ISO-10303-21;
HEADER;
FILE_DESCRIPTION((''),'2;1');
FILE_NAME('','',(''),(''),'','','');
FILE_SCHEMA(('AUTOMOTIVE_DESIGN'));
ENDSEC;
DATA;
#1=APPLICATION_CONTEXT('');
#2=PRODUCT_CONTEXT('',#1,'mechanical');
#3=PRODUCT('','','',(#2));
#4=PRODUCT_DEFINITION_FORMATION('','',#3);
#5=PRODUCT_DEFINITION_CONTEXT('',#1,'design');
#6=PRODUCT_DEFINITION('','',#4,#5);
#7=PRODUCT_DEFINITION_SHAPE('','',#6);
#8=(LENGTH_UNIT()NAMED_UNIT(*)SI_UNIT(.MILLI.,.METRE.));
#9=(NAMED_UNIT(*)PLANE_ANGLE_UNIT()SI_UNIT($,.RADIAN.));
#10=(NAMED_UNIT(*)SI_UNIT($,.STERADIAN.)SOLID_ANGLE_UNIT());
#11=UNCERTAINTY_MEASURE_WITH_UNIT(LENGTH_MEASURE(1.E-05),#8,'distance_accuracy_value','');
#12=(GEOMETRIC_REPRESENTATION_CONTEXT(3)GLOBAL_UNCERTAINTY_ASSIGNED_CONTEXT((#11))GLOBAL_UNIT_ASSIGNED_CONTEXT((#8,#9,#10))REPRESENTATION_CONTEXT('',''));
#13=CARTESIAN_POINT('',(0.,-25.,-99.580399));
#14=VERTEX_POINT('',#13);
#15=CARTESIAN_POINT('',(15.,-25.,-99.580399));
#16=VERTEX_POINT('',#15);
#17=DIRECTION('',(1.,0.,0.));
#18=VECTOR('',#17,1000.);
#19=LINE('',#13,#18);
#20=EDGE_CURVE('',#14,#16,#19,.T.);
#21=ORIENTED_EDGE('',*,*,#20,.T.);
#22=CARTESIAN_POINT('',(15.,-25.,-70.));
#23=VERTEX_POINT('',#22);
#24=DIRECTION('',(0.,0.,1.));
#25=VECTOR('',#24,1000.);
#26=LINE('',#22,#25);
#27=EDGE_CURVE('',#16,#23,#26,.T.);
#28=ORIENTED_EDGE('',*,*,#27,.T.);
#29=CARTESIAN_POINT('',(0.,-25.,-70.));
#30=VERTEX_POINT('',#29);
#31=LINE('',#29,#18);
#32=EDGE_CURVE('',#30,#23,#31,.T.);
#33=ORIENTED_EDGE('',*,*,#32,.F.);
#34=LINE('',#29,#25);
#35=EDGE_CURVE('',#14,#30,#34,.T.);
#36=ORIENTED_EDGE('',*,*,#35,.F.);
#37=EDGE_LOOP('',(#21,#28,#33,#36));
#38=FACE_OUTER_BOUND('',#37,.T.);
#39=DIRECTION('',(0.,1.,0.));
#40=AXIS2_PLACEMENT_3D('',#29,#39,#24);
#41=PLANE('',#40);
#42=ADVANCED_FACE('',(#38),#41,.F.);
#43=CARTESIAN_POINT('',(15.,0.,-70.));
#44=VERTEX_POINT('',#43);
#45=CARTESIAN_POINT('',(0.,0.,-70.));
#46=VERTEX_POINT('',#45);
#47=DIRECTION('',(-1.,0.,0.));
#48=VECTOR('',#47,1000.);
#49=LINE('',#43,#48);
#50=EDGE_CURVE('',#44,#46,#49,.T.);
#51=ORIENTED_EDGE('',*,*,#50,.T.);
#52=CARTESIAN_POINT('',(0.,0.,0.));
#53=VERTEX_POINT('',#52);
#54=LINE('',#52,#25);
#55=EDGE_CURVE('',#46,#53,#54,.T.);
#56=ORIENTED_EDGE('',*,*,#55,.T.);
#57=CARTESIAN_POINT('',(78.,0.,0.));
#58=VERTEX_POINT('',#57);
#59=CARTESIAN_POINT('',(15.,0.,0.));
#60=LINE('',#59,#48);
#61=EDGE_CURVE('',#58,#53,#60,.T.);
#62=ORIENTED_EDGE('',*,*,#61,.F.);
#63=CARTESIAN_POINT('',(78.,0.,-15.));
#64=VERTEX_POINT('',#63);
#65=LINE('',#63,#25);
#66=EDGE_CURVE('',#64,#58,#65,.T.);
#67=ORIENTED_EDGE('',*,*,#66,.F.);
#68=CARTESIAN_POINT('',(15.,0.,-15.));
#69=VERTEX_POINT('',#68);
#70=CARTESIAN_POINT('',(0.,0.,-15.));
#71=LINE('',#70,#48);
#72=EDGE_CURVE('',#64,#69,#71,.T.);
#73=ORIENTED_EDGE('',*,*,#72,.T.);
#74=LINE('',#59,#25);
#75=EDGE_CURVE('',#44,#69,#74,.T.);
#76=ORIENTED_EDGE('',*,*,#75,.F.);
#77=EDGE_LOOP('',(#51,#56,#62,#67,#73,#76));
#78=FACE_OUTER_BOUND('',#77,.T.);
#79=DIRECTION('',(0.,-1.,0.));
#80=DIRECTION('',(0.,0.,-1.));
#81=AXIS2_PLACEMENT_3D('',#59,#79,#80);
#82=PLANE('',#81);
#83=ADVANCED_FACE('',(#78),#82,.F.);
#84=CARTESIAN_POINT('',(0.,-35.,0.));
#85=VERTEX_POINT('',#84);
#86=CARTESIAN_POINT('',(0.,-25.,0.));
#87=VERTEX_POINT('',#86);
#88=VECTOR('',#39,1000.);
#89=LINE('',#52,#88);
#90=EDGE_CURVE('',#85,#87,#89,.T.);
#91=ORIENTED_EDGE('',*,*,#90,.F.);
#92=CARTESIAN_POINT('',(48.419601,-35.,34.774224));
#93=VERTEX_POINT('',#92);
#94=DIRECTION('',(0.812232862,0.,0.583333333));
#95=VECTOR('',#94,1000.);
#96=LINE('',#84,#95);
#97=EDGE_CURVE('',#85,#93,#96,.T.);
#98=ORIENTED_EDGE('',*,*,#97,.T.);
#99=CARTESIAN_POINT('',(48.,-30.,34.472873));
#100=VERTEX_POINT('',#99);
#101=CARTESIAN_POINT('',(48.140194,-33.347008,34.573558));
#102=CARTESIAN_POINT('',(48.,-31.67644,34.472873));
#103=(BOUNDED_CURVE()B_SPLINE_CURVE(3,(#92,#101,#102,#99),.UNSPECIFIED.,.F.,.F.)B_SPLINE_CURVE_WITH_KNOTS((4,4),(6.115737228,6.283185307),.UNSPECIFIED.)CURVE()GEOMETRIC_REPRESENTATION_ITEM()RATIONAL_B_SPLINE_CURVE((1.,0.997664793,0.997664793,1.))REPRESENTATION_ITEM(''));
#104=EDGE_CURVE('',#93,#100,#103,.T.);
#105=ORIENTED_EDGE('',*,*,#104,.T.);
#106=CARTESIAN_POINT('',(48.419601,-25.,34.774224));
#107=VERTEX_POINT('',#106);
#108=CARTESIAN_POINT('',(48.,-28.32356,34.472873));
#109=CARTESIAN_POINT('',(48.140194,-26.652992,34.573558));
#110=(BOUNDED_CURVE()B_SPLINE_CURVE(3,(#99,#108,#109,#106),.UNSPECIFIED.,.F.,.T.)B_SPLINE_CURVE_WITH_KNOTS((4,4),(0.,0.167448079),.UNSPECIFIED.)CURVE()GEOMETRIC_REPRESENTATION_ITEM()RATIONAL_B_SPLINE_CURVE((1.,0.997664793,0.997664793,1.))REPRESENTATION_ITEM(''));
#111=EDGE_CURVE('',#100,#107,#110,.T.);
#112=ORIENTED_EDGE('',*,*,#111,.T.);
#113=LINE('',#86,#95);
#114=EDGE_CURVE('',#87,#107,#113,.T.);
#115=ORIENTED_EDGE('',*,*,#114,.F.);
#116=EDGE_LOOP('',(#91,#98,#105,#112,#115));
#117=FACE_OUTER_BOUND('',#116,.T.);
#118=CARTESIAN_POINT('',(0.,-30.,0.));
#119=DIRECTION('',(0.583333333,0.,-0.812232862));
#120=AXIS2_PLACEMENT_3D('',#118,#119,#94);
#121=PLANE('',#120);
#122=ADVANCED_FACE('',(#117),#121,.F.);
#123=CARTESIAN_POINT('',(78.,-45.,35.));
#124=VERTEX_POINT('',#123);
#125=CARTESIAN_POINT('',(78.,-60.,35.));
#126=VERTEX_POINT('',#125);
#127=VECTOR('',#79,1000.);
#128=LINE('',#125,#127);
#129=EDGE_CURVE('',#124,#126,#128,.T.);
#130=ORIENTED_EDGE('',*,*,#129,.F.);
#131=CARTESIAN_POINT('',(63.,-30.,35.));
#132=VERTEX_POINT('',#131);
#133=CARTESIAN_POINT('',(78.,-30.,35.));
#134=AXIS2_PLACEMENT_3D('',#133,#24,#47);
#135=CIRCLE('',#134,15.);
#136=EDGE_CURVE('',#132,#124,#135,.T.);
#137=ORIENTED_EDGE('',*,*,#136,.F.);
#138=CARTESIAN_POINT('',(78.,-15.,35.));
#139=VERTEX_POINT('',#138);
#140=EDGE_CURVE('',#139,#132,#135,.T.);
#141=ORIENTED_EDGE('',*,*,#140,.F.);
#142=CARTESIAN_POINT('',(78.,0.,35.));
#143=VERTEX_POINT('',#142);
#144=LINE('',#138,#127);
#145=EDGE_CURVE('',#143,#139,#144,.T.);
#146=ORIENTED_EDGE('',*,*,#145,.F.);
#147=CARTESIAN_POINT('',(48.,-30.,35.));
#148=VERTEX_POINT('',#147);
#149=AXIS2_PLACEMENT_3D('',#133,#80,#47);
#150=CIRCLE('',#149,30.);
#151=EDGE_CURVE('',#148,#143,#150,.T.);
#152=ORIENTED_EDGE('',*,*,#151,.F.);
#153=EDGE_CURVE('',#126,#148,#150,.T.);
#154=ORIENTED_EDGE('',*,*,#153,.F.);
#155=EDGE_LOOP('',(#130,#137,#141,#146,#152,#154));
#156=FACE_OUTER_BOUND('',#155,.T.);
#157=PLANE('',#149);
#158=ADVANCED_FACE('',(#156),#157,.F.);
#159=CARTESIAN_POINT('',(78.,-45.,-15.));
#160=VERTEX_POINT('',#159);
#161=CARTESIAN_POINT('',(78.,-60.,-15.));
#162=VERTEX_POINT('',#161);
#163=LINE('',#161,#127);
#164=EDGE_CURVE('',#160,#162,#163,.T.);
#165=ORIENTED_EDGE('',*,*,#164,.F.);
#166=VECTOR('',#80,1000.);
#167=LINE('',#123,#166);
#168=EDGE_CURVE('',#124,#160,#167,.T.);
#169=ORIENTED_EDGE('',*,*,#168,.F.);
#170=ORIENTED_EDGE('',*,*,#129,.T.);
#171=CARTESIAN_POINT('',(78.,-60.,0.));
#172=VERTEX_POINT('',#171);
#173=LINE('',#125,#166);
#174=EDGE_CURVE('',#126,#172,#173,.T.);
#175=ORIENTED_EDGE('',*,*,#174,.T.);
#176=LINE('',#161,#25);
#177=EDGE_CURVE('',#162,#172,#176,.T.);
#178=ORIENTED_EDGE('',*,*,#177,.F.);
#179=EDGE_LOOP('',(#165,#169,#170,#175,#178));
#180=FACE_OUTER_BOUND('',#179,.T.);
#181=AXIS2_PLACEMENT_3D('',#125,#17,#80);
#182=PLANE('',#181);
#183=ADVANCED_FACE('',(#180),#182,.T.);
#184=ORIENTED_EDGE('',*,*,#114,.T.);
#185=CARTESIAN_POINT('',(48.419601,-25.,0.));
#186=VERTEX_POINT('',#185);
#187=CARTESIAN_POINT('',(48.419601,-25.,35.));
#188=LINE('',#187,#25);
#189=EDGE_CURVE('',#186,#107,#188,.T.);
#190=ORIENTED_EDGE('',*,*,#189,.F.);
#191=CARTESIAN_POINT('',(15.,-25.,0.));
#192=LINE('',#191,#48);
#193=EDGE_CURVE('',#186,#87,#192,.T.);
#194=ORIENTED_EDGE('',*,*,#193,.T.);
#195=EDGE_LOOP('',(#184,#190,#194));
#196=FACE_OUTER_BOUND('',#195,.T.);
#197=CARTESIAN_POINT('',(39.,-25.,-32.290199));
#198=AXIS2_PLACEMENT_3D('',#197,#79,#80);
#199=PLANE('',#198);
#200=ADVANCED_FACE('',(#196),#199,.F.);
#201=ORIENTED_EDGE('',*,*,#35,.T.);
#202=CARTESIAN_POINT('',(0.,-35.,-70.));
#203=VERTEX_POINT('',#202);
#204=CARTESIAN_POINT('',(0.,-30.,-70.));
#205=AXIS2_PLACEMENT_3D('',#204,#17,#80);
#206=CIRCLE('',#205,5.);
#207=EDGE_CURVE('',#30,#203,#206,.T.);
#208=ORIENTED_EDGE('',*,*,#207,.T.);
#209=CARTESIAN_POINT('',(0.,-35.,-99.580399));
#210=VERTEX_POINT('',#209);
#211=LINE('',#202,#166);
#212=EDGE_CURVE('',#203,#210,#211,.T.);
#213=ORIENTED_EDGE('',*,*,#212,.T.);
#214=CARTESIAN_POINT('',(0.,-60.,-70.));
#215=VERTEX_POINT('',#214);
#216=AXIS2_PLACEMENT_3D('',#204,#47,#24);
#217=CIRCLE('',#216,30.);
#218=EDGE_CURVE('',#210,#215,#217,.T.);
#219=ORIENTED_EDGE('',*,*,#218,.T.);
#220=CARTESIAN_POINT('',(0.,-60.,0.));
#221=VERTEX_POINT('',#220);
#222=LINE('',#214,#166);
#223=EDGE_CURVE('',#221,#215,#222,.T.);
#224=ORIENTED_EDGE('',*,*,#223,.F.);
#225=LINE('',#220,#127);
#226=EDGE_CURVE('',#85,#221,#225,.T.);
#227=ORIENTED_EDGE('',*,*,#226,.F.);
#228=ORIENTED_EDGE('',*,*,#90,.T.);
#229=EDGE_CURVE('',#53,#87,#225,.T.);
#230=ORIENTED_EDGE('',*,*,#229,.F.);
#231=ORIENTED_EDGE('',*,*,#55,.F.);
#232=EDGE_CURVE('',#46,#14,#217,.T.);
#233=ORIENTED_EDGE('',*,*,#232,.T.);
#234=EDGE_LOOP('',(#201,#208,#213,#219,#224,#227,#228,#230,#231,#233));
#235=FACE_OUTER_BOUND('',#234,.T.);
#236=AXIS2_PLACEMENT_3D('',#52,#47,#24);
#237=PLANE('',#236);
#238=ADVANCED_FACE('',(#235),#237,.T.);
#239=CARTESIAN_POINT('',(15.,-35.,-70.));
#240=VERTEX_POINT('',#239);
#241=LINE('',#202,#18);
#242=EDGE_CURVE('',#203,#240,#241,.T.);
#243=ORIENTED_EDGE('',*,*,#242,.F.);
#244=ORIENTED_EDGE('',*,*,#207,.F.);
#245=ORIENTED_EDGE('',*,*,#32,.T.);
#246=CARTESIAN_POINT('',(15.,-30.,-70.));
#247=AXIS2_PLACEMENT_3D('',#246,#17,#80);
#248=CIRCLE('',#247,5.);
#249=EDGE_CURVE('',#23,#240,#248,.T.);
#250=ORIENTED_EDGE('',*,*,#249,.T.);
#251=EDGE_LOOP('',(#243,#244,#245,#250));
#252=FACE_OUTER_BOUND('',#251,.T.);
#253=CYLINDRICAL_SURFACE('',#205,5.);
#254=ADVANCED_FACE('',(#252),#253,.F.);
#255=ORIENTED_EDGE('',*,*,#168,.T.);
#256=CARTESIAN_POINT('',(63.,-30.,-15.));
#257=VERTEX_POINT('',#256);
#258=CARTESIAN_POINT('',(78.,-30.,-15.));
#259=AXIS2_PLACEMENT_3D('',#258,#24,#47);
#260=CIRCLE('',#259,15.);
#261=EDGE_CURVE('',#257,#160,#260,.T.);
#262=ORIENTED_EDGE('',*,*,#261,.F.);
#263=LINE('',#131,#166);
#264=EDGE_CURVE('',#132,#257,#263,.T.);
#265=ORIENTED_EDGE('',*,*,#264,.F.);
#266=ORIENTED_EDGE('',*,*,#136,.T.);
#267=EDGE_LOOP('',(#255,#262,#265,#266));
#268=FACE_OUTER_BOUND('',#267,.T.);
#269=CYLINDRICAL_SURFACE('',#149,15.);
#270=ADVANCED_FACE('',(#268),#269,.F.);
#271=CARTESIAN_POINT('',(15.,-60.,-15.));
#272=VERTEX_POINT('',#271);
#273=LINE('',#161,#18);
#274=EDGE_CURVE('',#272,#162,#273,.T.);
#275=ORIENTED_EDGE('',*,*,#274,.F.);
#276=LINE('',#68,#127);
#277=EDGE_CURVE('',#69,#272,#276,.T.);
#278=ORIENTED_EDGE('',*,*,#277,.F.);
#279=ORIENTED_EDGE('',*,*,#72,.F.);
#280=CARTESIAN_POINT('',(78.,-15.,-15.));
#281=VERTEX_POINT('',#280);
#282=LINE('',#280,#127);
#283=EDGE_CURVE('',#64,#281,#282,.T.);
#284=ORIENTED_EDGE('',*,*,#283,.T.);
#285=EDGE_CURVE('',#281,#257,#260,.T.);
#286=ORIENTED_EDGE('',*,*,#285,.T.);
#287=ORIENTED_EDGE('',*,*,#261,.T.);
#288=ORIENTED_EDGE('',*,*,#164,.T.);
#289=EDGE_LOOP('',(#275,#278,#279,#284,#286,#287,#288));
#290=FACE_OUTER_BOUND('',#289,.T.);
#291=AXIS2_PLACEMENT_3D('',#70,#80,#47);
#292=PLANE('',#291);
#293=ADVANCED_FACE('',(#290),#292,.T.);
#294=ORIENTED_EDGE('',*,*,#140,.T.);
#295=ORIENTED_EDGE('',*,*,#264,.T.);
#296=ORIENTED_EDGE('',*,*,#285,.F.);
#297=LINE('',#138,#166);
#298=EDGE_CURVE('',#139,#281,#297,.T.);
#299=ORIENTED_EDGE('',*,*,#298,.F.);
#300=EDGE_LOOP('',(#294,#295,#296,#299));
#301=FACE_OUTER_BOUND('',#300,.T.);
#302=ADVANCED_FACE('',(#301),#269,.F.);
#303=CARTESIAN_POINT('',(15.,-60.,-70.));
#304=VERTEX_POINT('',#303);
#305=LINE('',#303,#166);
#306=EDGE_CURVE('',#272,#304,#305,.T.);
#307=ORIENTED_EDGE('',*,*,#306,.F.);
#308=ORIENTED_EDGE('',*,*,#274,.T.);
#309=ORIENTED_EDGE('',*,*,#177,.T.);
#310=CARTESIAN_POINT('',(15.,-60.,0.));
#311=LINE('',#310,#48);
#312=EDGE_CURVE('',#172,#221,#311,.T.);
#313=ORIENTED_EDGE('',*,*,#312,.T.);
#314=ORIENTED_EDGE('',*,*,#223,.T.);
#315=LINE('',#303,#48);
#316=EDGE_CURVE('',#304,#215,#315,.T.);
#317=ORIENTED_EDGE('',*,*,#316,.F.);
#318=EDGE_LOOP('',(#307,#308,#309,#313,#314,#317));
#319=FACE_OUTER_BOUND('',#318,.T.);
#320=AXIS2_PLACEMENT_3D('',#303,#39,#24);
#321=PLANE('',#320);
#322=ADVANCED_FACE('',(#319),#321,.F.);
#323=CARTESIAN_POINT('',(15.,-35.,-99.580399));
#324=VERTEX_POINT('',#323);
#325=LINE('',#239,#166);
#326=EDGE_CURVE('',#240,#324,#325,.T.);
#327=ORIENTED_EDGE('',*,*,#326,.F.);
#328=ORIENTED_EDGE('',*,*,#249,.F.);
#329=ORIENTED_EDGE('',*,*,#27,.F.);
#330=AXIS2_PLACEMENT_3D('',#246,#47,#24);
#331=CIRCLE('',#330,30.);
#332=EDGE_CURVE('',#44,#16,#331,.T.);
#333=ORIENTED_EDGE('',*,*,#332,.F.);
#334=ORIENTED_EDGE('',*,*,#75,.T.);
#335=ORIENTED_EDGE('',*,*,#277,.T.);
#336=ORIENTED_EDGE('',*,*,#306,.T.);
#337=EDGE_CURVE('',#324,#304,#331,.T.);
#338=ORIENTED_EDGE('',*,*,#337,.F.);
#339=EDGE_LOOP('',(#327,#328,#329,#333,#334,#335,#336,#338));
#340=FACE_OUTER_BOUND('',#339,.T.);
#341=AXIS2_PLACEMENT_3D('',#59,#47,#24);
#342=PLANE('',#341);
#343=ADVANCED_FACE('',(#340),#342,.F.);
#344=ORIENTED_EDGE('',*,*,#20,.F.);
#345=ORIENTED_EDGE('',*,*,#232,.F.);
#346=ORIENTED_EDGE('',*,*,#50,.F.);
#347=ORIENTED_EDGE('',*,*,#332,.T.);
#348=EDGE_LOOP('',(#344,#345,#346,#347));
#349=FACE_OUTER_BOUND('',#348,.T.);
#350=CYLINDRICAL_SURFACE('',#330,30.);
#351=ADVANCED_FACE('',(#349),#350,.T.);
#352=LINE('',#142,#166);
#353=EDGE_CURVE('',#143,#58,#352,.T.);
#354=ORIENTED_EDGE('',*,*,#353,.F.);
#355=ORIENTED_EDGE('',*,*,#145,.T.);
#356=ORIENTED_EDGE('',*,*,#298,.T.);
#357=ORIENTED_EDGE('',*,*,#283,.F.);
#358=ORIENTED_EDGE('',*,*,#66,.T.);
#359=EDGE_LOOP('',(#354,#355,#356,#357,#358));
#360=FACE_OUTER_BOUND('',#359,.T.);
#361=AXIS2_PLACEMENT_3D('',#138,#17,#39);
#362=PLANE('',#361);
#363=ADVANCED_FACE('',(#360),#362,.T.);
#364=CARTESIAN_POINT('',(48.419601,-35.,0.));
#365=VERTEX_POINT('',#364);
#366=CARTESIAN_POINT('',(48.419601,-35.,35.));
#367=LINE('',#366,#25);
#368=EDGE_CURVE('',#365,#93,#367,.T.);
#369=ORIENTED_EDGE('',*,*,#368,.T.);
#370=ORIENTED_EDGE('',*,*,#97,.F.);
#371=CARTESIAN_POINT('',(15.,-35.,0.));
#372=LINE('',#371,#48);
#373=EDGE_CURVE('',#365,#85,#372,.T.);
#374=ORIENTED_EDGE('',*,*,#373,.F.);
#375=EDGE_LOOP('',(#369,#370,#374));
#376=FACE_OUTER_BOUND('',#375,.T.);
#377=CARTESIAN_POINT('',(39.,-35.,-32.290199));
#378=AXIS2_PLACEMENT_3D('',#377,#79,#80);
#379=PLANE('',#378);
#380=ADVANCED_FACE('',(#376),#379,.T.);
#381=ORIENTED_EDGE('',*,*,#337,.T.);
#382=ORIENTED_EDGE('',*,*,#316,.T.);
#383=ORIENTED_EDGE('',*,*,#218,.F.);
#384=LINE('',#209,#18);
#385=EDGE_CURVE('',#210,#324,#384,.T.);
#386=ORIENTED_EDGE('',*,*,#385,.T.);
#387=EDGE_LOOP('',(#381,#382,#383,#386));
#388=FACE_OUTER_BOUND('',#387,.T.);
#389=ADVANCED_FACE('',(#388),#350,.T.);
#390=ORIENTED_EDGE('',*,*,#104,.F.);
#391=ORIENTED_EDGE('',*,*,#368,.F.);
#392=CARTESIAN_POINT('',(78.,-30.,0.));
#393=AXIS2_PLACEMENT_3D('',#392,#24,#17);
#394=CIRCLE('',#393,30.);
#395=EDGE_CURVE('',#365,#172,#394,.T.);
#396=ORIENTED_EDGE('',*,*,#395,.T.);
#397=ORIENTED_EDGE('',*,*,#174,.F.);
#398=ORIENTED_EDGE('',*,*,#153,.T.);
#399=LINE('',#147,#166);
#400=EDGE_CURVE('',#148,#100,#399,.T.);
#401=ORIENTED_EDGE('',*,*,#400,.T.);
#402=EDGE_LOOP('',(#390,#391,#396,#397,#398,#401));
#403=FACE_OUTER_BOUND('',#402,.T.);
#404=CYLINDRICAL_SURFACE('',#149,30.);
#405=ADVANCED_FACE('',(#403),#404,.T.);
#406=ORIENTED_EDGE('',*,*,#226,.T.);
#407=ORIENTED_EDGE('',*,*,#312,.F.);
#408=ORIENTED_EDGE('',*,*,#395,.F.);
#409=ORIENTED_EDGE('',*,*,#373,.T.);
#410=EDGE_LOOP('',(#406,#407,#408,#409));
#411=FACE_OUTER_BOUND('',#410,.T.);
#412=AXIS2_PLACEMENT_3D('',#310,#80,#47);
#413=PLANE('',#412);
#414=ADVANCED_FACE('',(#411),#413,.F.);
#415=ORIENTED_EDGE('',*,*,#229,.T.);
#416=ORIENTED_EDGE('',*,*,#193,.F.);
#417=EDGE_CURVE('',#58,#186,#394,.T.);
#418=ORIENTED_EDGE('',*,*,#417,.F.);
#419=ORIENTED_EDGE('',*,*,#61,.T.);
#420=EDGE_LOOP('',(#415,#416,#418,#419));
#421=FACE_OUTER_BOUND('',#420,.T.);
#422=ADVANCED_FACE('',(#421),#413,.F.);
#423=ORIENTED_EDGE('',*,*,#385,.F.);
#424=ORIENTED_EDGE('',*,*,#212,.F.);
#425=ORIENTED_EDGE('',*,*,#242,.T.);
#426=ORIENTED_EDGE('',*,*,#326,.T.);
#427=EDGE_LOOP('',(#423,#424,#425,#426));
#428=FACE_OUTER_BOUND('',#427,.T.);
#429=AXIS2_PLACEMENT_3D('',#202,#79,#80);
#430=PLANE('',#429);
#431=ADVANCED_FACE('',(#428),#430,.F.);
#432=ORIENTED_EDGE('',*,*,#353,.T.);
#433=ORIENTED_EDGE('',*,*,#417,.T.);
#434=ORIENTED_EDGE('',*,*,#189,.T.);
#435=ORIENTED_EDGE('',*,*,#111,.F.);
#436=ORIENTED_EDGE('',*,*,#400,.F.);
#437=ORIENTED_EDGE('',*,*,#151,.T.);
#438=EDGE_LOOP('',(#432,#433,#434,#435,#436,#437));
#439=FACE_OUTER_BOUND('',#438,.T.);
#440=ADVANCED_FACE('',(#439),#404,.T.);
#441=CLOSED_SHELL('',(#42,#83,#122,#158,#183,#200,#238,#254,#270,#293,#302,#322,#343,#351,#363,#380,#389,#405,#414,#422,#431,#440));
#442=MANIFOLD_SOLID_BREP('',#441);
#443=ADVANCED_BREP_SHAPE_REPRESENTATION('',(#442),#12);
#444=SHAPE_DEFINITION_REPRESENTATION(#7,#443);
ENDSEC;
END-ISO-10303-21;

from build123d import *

# Parameters (mm, degrees)
BASE_BLOCK_SKETCH_W       = 70
BASE_BLOCK_SKETCH_H       = 60
BASE_BLOCK_60X70X15_DEPTH = 15
UPPER_ROUND_LUG_DEPTH     = 15
UPPER_SLOT_10MM_DEPTH     = 15
TOP_PLATE_SKETCH_W        = 78
TOP_PLATE_SKETCH_H        = 60
TOP_PLATE_78MM_DEPTH      = 15
RADIUS_CUT_SKETCH_R       = 30
RADIUS_CUT_DEPTH          = 15
LOWER_START               = -50
LOWER_LUG_50MM_DEPTH      = 50
SUPPORT_RIB_10MM_REACH    = 132.001
RIB_SKETCH_WALL_W         = 322.001968056
RIB_SKETCH_WALL_H         = 10


with BuildPart() as part:
    # Base Block Sketch → Base Block 60x70x15 (new body)
    with BuildSketch(Plane(origin=(0, 0, 0), x_dir=(0, 0, -1), z_dir=(1, 0, 0))):
        with Locations((35, -30)):
            Rectangle(BASE_BLOCK_SKETCH_W, BASE_BLOCK_SKETCH_H)
    extrude(amount=BASE_BLOCK_60X70X15_DEPTH)

    # Upper Lug Sketch → Upper Round Lug (add)
    with BuildSketch(Plane.ZY):
        with BuildLine():
            Line((-70, 0), (-70, -60))
            ThreePointArc((-70, -60), (-100, -30), (-70, 0))
        make_face()
    extrude(amount=-UPPER_ROUND_LUG_DEPTH)

    # Upper Slot Sketch → Upper Slot 10mm (cut)
    with BuildSketch(Plane(origin=(15, 0, 0), x_dir=(0, 0, -1), z_dir=(1, 0, 0))):
        with BuildLine():
            Line((70, -25), (99.580398915, -25))
            ThreePointArc((99.580398915, -25), (104.580398915, -30), (99.580398915, -35))
            Line((99.580398915, -35), (70, -35))
            ThreePointArc((70, -35), (65, -30), (70, -25))
        make_face()
    extrude(amount=-UPPER_SLOT_10MM_DEPTH, mode=Mode.SUBTRACT)

    # Top Plate Sketch → Top Plate 78mm (add)
    with BuildSketch(Plane.XY):
        with Locations((39, -30)):
            Rectangle(TOP_PLATE_SKETCH_W, TOP_PLATE_SKETCH_H)
    extrude(amount=-TOP_PLATE_78MM_DEPTH)

    # Radius Cut Sketch → Radius Cut (cut)
    with BuildSketch(Plane.XY):
        with Locations((78, -30)):
            Circle(RADIUS_CUT_SKETCH_R)
    extrude(amount=-RADIUS_CUT_DEPTH, mode=Mode.SUBTRACT)

    # Lower Lug Sketch → Lower Lug 50mm (add)
    with BuildSketch(Plane(origin=(0, 0, -15), x_dir=(-1, 0, 0), z_dir=(0, 0, -1)).offset(LOWER_START)):
        with BuildLine():
            Line((-78, -60), (-78, -45))
            ThreePointArc((-78, -45), (-63, -30), (-78, -15))
            Line((-78, -15), (-78, 0))
            ThreePointArc((-78, 0), (-48, -30), (-78, -60))
        make_face()
    extrude(amount=LOWER_LUG_50MM_DEPTH)

    # Rib Sketch wall → Support Rib 10mm (add, up to next)
    with BuildSketch(Plane(origin=(24.366985862, -30, 17.5), x_dir=(0.812232862067, 0, 0.583333333334), z_dir=(-0.583333333334, 0, 0.812232862067)), mode=Mode.PRIVATE) as support_rib_10mm_sk1:
        Rectangle(RIB_SKETCH_WALL_W, RIB_SKETCH_WALL_H)
    support_rib_10mm_tool1 = extrude(support_rib_10mm_sk1.sketch, amount=-SUPPORT_RIB_10MM_REACH, mode=Mode.PRIVATE) - part.part
    add(support_rib_10mm_tool1.solids().sort_by_distance((24.366985862, -30, 17.5))[0])


solid = part.part
